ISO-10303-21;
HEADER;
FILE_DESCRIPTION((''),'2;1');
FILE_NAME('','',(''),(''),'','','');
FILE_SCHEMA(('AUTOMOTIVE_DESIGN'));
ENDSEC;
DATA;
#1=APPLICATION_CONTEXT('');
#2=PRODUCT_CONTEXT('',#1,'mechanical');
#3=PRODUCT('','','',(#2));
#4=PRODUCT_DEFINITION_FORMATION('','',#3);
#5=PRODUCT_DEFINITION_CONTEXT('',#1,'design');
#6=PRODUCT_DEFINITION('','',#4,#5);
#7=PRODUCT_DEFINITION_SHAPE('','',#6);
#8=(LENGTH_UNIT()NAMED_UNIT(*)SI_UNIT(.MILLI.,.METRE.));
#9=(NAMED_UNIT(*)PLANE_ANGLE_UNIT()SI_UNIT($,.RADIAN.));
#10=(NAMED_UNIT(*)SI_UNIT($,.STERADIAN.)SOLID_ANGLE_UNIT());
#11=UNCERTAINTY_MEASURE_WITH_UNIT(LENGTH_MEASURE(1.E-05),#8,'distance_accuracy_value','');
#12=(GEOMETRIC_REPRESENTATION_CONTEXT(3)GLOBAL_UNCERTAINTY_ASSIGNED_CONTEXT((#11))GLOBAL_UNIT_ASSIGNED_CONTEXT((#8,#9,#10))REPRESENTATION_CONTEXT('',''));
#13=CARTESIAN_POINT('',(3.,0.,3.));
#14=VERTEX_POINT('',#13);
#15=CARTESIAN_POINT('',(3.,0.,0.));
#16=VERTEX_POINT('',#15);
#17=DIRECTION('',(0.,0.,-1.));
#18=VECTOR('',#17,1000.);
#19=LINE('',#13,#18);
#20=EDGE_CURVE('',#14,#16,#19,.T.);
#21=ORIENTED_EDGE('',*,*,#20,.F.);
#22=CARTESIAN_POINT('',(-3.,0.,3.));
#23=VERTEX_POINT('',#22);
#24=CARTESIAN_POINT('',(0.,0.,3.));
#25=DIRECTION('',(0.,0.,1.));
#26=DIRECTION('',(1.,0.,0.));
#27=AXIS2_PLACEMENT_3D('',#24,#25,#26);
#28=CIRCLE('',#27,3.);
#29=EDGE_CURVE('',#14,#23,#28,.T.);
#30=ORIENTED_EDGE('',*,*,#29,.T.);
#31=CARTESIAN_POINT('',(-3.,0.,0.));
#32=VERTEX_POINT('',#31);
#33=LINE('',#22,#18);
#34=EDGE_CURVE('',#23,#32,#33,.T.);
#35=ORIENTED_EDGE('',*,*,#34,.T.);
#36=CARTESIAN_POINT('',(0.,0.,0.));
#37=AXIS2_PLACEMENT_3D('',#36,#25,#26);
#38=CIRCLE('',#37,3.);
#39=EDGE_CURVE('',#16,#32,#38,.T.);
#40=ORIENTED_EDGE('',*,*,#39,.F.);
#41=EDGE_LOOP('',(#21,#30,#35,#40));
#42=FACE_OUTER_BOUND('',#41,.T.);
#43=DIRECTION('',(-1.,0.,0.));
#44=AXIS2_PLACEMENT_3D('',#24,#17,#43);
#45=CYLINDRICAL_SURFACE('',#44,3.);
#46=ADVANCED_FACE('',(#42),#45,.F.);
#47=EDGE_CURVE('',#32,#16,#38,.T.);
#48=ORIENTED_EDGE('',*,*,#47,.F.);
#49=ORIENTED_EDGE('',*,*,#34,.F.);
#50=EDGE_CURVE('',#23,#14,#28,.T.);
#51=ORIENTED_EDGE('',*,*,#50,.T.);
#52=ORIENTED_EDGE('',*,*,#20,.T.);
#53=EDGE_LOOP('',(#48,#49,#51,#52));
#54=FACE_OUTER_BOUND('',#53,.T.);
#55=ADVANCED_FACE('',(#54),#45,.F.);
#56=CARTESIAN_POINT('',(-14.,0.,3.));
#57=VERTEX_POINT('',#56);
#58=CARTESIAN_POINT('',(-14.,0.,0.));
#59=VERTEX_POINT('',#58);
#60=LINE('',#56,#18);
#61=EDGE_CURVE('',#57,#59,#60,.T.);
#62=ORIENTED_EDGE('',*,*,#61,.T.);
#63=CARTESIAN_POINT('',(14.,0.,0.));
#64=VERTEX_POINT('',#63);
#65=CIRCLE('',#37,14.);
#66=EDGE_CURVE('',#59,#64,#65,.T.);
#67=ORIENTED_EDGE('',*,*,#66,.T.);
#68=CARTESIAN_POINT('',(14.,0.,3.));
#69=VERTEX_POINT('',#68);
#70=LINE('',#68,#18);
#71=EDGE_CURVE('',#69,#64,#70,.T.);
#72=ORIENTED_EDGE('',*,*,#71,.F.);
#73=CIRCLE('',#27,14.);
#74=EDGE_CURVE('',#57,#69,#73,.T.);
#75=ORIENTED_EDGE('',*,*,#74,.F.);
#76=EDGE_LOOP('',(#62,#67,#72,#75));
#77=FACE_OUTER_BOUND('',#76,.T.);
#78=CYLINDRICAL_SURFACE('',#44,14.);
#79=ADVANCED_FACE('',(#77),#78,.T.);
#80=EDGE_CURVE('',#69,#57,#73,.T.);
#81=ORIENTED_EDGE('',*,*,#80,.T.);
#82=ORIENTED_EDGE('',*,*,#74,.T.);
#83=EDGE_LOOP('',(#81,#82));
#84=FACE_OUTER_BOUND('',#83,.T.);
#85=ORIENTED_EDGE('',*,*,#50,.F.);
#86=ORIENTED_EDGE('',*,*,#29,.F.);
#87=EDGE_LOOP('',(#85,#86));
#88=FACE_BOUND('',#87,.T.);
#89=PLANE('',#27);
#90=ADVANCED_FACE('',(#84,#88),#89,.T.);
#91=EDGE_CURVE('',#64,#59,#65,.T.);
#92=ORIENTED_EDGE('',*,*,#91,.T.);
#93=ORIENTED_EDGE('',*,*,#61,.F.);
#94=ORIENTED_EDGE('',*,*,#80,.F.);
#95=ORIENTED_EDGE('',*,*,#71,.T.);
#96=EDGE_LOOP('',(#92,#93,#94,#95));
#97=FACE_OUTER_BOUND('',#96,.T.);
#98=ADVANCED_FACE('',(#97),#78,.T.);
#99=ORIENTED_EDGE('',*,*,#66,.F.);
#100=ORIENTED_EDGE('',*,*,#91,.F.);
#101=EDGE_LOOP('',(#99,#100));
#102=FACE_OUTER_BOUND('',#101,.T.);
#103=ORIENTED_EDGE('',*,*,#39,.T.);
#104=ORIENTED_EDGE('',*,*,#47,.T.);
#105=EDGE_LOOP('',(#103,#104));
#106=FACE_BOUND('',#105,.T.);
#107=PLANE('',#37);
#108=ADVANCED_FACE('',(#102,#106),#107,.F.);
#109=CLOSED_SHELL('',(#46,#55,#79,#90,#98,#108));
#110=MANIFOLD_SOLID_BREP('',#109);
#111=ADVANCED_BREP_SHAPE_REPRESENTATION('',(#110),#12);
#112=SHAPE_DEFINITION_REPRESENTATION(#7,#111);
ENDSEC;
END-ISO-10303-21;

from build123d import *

# Parameters (mm, degrees)
SKETCH1_R           = 14
SKETCH1_R_2         = 3
BOSS_EXTRUDE1_DEPTH = 3


with BuildPart() as part:
    # Sketch1 → Boss-Extrude1 (new body)
    with BuildSketch(Plane.XY):
        Circle(SKETCH1_R)
        Circle(SKETCH1_R_2, mode=Mode.SUBTRACT)
    extrude(amount=BOSS_EXTRUDE1_DEPTH)


solid = part.part
